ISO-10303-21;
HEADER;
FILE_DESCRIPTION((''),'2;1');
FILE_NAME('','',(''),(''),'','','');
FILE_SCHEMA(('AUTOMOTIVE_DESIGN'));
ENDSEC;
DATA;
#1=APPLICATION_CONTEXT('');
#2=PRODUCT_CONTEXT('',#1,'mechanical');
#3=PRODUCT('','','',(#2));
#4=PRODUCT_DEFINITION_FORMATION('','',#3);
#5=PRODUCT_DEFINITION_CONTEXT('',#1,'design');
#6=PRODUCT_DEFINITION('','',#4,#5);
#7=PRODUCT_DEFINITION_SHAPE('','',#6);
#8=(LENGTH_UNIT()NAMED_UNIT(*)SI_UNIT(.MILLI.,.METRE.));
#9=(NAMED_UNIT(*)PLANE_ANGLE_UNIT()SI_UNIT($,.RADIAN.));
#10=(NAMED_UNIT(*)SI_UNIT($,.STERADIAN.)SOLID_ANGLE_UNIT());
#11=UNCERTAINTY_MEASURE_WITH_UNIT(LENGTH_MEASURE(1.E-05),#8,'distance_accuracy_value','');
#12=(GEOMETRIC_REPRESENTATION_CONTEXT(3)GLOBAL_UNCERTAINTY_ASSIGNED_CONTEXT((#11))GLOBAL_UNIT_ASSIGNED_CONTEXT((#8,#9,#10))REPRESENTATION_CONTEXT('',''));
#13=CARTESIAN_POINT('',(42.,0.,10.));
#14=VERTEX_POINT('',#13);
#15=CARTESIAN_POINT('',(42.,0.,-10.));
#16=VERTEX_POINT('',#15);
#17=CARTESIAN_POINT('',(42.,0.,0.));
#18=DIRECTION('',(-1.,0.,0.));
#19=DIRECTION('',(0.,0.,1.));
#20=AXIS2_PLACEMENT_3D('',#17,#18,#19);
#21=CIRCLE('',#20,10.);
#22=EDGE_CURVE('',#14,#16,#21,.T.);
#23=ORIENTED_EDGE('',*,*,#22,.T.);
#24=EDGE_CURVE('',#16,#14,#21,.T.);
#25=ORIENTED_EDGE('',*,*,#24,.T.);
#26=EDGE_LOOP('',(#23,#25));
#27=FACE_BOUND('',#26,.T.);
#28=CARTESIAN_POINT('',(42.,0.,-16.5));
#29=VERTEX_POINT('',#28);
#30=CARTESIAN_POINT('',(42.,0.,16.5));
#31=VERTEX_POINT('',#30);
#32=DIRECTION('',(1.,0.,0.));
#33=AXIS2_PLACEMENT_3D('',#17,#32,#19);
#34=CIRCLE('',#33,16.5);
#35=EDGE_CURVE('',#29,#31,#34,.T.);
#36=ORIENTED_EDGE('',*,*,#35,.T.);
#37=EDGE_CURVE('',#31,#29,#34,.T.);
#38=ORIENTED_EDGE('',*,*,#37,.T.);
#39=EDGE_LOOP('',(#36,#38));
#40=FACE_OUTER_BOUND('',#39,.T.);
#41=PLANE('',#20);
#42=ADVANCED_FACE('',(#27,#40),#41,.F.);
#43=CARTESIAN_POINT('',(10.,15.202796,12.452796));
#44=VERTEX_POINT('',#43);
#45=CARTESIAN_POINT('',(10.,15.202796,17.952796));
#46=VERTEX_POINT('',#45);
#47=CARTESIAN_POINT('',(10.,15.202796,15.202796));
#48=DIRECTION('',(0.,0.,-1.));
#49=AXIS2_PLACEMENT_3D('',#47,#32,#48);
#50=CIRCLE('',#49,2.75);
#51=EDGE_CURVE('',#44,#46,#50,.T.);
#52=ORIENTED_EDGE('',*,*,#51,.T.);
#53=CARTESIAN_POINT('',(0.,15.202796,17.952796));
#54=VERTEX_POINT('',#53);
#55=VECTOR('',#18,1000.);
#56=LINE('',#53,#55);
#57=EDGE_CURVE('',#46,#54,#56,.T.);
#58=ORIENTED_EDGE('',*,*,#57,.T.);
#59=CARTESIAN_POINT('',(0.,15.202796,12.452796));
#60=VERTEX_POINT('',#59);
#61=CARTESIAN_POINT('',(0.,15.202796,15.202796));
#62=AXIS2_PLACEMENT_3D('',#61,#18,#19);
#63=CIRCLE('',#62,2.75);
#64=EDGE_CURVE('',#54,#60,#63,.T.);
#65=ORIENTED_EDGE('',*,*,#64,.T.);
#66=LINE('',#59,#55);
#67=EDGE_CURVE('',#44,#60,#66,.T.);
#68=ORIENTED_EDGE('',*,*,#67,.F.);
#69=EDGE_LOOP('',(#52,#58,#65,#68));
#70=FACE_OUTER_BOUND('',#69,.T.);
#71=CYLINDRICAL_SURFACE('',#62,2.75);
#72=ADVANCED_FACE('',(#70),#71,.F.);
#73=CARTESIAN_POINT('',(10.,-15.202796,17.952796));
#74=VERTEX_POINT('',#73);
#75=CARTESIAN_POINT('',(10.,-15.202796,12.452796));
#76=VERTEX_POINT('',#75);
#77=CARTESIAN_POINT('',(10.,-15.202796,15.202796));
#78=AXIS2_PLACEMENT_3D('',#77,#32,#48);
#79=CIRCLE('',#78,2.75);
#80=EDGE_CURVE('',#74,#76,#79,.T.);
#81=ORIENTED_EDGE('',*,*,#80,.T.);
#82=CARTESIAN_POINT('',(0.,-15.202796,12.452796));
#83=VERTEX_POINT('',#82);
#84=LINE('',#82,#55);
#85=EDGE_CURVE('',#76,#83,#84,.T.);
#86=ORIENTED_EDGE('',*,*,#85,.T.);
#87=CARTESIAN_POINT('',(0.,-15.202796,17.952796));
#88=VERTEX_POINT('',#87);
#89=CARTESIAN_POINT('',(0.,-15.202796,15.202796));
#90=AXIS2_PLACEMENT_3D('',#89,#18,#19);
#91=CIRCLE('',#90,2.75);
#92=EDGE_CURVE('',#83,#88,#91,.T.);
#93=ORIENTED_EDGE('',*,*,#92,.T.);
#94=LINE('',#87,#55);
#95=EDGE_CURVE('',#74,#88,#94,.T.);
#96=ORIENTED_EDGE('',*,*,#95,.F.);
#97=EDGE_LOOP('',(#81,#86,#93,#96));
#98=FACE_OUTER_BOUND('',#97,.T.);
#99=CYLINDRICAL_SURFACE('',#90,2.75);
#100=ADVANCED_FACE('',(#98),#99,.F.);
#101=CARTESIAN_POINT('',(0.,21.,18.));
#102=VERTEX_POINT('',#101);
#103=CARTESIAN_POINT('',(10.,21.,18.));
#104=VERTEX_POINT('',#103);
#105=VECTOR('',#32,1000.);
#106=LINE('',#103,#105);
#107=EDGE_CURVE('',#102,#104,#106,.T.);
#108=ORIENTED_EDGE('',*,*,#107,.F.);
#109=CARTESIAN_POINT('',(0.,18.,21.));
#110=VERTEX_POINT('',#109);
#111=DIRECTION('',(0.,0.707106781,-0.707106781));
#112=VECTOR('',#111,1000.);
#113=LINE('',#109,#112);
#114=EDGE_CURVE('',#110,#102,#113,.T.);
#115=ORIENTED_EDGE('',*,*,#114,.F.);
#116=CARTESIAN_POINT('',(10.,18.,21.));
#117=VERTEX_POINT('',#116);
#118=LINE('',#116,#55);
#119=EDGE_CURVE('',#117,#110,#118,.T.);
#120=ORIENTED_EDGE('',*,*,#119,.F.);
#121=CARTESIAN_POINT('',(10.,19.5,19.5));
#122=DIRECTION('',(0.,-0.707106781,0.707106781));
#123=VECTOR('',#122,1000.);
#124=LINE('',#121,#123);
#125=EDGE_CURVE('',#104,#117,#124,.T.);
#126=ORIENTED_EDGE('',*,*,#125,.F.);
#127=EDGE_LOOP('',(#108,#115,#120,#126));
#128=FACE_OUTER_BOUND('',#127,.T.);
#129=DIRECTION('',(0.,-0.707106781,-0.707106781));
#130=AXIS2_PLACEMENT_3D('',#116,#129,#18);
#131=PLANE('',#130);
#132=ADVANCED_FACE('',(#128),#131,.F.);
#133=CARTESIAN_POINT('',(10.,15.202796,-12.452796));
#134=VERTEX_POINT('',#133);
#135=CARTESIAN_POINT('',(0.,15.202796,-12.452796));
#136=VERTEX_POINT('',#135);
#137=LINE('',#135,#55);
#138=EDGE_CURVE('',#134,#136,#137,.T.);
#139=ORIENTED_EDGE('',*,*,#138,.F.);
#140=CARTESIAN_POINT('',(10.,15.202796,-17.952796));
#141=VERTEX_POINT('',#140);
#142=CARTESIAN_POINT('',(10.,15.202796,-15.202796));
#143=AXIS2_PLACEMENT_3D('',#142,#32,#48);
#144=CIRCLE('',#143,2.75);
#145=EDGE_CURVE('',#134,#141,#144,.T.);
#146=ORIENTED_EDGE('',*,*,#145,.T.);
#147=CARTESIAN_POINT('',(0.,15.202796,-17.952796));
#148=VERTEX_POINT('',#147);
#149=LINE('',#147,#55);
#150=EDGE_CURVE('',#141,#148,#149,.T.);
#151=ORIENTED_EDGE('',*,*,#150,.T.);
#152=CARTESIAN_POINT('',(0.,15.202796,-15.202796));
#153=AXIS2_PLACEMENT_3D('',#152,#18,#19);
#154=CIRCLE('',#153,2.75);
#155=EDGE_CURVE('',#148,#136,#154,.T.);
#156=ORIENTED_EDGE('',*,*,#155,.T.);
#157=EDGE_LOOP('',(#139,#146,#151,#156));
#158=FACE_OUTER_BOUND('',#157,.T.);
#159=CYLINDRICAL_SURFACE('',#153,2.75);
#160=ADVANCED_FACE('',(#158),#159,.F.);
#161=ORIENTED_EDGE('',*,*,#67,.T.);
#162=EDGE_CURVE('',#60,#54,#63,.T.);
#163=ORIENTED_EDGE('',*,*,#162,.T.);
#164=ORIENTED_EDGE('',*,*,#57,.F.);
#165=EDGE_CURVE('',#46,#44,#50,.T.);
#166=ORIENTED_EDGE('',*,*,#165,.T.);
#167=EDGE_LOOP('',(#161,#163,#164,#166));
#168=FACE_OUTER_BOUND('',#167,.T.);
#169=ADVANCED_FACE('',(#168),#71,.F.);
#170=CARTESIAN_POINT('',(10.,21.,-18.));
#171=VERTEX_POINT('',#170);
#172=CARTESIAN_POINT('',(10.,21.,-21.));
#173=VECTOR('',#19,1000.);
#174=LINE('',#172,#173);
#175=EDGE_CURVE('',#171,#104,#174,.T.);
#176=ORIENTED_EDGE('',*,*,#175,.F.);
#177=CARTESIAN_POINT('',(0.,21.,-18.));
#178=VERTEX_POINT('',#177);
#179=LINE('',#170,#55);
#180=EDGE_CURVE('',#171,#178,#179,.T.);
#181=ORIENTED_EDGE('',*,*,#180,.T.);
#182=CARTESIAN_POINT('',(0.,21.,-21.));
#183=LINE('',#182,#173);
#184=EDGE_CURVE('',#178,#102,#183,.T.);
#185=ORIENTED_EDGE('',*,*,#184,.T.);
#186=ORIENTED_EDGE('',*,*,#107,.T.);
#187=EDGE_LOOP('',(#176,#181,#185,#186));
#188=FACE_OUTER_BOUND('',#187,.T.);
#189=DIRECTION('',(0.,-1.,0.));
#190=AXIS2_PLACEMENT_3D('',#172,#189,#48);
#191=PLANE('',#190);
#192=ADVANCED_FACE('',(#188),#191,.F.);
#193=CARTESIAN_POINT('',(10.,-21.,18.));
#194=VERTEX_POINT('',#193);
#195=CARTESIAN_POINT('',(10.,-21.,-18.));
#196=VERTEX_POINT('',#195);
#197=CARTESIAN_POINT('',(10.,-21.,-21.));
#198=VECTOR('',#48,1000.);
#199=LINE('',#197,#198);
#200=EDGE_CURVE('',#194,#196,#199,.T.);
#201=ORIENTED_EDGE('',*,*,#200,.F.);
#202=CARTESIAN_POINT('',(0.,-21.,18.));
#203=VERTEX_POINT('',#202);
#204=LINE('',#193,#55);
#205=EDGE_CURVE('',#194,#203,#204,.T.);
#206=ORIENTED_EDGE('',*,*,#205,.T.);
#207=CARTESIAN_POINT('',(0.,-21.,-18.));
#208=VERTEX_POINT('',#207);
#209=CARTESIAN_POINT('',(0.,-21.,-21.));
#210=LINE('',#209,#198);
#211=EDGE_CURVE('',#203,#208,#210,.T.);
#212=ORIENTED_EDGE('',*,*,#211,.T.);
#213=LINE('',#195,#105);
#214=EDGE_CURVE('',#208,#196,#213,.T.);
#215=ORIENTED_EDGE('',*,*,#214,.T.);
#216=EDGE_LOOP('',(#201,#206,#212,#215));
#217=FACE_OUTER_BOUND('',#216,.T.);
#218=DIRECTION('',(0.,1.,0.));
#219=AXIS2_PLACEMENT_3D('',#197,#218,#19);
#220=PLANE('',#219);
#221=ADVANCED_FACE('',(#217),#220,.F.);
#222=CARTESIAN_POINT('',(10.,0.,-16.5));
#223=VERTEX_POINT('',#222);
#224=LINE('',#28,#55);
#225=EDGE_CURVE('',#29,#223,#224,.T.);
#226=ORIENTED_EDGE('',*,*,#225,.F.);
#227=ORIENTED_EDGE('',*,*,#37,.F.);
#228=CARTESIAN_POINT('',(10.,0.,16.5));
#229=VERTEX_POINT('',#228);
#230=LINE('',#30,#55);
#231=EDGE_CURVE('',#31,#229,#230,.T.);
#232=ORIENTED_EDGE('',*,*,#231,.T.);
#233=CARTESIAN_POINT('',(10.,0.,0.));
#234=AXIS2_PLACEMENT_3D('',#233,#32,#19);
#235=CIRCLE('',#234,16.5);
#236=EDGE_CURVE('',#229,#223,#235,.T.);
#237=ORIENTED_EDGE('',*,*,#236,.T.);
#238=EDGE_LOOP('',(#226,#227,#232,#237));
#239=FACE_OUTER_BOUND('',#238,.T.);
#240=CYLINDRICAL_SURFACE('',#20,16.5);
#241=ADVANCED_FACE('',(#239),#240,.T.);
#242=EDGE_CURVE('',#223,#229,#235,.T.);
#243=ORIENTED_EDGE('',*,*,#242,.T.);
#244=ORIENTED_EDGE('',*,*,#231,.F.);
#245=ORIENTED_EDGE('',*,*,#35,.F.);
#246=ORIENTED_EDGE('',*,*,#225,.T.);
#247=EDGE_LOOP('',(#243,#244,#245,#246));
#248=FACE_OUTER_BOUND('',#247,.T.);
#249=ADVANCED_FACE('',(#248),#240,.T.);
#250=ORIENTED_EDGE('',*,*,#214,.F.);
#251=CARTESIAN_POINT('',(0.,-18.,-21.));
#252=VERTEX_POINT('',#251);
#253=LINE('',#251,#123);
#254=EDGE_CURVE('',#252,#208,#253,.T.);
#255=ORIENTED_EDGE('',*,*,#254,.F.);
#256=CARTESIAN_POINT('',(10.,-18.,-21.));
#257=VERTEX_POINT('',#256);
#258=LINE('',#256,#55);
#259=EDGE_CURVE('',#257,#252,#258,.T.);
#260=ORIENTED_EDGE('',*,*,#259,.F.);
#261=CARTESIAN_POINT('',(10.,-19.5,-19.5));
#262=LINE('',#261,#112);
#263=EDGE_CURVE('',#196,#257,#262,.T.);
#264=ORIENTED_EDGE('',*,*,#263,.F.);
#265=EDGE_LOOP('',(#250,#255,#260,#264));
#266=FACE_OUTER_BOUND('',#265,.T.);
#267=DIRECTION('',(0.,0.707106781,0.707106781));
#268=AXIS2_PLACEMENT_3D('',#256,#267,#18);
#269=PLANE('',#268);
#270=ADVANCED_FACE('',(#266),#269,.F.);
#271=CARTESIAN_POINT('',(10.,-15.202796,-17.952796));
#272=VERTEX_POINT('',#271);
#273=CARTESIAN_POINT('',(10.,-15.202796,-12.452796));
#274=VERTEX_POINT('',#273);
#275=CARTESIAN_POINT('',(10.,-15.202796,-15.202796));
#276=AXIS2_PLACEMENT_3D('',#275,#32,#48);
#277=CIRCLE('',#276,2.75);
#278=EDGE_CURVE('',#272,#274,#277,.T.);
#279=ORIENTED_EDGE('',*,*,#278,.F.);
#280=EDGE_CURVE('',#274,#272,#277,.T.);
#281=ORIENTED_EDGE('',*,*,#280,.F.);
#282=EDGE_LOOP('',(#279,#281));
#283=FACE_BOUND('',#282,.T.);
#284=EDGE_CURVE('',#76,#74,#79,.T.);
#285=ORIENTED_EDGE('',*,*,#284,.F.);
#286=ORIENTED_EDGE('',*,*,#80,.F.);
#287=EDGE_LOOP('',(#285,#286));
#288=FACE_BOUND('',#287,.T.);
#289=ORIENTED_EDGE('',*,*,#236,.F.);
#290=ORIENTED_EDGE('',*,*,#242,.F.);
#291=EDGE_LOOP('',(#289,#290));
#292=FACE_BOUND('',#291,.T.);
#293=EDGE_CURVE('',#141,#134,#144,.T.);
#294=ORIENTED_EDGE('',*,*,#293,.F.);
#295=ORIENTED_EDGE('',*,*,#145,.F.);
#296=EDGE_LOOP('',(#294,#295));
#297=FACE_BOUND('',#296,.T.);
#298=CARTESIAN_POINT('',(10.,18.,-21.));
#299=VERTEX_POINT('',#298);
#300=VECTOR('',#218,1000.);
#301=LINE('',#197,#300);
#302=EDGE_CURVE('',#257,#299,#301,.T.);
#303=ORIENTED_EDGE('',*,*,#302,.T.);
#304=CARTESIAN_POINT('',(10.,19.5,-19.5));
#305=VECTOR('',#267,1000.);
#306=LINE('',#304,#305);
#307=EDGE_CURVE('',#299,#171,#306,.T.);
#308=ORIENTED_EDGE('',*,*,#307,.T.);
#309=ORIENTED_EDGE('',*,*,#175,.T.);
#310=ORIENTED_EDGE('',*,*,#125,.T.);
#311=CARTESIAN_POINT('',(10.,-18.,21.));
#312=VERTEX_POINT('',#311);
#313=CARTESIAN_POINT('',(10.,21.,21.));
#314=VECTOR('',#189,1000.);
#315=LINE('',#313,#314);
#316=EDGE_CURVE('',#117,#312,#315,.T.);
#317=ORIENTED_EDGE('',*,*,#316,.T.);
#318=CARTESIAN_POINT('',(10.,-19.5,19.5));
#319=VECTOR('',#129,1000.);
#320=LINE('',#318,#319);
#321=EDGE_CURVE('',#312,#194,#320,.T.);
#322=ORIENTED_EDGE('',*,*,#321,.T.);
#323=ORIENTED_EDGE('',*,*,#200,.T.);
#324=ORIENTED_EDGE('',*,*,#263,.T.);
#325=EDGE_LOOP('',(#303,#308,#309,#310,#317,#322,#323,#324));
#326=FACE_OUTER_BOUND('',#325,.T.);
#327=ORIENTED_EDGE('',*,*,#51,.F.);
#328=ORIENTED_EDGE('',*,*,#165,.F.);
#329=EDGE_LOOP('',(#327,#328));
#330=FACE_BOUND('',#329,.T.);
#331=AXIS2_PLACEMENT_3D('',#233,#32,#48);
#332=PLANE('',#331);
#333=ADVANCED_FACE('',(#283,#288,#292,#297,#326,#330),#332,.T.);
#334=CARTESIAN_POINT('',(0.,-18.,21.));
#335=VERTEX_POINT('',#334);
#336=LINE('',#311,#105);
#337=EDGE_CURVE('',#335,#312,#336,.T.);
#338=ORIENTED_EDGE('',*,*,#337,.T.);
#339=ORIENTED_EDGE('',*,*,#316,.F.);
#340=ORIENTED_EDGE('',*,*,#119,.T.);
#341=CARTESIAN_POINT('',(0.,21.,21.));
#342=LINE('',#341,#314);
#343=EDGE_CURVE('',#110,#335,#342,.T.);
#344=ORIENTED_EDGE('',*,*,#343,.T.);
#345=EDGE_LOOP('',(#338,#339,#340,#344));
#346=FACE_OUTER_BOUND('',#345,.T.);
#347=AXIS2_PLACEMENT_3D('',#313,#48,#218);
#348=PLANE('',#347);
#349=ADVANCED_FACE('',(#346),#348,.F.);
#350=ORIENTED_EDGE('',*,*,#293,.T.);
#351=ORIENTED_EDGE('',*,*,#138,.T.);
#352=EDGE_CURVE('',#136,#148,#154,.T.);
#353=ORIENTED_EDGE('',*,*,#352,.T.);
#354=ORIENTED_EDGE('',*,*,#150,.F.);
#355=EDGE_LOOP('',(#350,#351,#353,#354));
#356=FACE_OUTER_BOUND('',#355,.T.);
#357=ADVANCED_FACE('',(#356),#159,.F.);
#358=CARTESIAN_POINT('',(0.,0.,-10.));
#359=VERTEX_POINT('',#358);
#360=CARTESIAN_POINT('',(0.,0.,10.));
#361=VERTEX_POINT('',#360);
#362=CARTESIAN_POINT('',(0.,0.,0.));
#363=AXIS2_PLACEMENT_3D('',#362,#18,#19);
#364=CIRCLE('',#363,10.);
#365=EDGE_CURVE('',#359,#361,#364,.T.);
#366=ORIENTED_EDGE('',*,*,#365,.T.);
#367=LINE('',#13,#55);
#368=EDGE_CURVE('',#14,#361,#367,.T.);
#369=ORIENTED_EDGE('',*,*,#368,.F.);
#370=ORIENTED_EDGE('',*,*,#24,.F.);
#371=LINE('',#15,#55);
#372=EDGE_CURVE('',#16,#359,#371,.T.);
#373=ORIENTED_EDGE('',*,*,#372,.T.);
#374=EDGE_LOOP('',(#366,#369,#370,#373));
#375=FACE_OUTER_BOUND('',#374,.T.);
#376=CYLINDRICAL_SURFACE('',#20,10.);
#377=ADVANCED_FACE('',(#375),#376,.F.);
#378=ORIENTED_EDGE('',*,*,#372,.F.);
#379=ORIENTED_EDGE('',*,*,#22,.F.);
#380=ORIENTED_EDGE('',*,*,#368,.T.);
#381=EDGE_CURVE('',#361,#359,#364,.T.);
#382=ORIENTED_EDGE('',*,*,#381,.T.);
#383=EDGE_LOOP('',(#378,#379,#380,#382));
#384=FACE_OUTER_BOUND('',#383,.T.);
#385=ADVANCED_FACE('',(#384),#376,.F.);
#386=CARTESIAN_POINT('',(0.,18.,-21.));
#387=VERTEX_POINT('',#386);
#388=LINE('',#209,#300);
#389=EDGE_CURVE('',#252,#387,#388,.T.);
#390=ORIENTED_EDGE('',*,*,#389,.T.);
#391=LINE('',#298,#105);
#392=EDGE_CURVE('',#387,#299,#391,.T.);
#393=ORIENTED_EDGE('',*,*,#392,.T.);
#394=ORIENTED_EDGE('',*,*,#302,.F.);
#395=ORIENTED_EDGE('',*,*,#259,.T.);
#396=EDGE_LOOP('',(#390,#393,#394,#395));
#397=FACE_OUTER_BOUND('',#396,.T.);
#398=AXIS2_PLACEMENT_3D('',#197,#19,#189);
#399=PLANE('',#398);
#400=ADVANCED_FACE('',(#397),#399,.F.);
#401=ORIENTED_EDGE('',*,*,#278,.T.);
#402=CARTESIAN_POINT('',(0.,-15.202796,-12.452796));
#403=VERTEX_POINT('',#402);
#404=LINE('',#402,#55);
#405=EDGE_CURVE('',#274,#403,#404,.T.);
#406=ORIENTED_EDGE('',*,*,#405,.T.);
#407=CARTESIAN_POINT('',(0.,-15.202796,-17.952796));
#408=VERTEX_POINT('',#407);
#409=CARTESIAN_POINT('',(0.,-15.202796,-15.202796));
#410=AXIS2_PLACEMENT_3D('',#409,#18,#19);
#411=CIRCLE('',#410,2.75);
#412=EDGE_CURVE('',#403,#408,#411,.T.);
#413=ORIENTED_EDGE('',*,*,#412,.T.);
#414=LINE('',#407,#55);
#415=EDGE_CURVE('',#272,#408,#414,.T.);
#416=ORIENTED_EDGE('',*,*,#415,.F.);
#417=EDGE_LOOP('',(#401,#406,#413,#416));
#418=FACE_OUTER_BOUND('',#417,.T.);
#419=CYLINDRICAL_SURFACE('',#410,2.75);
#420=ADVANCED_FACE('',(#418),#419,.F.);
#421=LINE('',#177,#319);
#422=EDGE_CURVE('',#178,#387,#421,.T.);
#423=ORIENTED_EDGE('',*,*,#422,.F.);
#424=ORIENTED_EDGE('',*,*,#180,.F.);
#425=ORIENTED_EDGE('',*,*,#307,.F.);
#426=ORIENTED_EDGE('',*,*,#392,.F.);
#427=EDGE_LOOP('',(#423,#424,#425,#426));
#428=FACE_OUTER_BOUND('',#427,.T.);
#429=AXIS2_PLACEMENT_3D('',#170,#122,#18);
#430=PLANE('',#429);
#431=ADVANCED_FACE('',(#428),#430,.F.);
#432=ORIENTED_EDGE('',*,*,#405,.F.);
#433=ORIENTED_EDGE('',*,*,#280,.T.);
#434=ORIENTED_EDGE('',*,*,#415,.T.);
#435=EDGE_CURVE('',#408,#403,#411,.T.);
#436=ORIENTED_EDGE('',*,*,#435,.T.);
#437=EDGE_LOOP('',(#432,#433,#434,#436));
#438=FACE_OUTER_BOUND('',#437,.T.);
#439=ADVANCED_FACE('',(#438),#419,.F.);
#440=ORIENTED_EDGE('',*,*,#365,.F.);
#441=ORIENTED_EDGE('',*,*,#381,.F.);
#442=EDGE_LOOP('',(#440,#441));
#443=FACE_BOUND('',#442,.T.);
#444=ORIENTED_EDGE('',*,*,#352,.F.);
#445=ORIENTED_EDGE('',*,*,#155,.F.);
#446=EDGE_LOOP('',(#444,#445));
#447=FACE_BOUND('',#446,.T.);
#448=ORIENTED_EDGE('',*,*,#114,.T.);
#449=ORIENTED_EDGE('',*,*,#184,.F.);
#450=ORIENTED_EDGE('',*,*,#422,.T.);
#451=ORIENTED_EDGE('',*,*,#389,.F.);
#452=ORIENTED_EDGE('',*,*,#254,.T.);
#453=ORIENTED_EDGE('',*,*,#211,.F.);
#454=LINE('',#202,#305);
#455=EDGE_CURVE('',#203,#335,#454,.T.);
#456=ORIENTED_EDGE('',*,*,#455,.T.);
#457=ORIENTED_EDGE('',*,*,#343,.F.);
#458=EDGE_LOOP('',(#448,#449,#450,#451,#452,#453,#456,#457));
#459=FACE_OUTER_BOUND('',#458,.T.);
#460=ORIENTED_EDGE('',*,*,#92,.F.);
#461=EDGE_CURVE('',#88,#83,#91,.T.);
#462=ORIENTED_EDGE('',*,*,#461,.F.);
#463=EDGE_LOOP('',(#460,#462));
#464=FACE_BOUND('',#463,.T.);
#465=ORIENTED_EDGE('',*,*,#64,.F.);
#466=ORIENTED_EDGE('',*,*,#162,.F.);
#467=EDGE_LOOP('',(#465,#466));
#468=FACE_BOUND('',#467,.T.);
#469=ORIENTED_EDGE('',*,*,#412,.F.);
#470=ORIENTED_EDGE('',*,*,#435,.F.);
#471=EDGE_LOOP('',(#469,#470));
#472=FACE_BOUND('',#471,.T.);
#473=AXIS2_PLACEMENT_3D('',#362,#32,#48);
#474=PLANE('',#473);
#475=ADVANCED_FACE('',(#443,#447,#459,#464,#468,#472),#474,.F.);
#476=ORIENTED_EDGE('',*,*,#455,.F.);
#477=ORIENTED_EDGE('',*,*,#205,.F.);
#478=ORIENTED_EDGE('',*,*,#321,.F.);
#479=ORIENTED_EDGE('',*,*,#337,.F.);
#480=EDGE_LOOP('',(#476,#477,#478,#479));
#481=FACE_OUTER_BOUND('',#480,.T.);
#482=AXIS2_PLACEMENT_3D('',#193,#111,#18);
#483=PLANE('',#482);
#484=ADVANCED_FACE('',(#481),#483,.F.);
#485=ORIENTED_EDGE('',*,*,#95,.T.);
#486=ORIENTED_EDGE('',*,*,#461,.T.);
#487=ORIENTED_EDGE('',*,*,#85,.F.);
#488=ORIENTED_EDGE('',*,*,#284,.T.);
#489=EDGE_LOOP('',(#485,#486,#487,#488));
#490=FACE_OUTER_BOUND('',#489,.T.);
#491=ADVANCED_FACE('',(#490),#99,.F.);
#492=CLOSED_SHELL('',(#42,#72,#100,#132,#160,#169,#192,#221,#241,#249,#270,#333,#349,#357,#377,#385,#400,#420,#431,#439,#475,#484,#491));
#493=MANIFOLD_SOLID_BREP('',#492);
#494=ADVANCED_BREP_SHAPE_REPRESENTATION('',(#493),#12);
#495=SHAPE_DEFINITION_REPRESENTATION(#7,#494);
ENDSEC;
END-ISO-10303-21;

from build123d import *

# Parameters (mm, degrees)
SKETCH1_W                  = 42
SKETCH1_H                  = 42
BOSS_EXTRUDE1_DEPTH        = 10
SKETCH2_R                  = 16.5
BOSS_EXTRUDE2_DEPTH        = 32
F_5_5_5_5_DIAMETER_HOLE1_D = 5.5
SKETCH7_R                  = 10
CUT_EXTRUDE1_DEPTH         = 52.439284598
CHAMFER1_SIZE              = 3


with BuildPart() as part:
    # Sketch1 → Boss-Extrude1 (new body)
    with BuildSketch(Plane(origin=(0, 0, 0), x_dir=(0, 0, -1), z_dir=(1, 0, 0))):
        Rectangle(SKETCH1_W, SKETCH1_H)
    extrude(amount=BOSS_EXTRUDE1_DEPTH)

    # Sketch2 → Boss-Extrude2 (add)
    with BuildSketch(Plane(origin=(10, 0, 0), x_dir=(0, 0, -1), z_dir=(1, 0, 0))):
        with Locations(Location((0, 0, 0), (0, 0, 180))):
            Circle(SKETCH2_R)
    extrude(amount=BOSS_EXTRUDE2_DEPTH)

    # Ø5.5 (5.5) Diameter Hole1 (through all)
    with Locations(Plane.ZY):
        with Locations((-15.202795796, 15.202795796), (15.202795796, 15.202795796), (15.202795796, -15.202795796), (-15.202795796, -15.202795796)):
            Hole(F_5_5_5_5_DIAMETER_HOLE1_D / 2)

    # Sketch7 → Cut-Extrude1 (cut, through all)
    with BuildSketch(Plane.ZY):
        Circle(SKETCH7_R)
    extrude(amount=-CUT_EXTRUDE1_DEPTH, mode=Mode.SUBTRACT)

    # Chamfer1
    chamfer1_edges = [part.edges().sort_by_distance(p)[0] for p in [
        (5, 21, -21),
        (5, -21, -21),
        (5, -21, 21),
        (5, 21, 21),
    ]]
    chamfer(chamfer1_edges, length=CHAMFER1_SIZE)


solid = part.part
